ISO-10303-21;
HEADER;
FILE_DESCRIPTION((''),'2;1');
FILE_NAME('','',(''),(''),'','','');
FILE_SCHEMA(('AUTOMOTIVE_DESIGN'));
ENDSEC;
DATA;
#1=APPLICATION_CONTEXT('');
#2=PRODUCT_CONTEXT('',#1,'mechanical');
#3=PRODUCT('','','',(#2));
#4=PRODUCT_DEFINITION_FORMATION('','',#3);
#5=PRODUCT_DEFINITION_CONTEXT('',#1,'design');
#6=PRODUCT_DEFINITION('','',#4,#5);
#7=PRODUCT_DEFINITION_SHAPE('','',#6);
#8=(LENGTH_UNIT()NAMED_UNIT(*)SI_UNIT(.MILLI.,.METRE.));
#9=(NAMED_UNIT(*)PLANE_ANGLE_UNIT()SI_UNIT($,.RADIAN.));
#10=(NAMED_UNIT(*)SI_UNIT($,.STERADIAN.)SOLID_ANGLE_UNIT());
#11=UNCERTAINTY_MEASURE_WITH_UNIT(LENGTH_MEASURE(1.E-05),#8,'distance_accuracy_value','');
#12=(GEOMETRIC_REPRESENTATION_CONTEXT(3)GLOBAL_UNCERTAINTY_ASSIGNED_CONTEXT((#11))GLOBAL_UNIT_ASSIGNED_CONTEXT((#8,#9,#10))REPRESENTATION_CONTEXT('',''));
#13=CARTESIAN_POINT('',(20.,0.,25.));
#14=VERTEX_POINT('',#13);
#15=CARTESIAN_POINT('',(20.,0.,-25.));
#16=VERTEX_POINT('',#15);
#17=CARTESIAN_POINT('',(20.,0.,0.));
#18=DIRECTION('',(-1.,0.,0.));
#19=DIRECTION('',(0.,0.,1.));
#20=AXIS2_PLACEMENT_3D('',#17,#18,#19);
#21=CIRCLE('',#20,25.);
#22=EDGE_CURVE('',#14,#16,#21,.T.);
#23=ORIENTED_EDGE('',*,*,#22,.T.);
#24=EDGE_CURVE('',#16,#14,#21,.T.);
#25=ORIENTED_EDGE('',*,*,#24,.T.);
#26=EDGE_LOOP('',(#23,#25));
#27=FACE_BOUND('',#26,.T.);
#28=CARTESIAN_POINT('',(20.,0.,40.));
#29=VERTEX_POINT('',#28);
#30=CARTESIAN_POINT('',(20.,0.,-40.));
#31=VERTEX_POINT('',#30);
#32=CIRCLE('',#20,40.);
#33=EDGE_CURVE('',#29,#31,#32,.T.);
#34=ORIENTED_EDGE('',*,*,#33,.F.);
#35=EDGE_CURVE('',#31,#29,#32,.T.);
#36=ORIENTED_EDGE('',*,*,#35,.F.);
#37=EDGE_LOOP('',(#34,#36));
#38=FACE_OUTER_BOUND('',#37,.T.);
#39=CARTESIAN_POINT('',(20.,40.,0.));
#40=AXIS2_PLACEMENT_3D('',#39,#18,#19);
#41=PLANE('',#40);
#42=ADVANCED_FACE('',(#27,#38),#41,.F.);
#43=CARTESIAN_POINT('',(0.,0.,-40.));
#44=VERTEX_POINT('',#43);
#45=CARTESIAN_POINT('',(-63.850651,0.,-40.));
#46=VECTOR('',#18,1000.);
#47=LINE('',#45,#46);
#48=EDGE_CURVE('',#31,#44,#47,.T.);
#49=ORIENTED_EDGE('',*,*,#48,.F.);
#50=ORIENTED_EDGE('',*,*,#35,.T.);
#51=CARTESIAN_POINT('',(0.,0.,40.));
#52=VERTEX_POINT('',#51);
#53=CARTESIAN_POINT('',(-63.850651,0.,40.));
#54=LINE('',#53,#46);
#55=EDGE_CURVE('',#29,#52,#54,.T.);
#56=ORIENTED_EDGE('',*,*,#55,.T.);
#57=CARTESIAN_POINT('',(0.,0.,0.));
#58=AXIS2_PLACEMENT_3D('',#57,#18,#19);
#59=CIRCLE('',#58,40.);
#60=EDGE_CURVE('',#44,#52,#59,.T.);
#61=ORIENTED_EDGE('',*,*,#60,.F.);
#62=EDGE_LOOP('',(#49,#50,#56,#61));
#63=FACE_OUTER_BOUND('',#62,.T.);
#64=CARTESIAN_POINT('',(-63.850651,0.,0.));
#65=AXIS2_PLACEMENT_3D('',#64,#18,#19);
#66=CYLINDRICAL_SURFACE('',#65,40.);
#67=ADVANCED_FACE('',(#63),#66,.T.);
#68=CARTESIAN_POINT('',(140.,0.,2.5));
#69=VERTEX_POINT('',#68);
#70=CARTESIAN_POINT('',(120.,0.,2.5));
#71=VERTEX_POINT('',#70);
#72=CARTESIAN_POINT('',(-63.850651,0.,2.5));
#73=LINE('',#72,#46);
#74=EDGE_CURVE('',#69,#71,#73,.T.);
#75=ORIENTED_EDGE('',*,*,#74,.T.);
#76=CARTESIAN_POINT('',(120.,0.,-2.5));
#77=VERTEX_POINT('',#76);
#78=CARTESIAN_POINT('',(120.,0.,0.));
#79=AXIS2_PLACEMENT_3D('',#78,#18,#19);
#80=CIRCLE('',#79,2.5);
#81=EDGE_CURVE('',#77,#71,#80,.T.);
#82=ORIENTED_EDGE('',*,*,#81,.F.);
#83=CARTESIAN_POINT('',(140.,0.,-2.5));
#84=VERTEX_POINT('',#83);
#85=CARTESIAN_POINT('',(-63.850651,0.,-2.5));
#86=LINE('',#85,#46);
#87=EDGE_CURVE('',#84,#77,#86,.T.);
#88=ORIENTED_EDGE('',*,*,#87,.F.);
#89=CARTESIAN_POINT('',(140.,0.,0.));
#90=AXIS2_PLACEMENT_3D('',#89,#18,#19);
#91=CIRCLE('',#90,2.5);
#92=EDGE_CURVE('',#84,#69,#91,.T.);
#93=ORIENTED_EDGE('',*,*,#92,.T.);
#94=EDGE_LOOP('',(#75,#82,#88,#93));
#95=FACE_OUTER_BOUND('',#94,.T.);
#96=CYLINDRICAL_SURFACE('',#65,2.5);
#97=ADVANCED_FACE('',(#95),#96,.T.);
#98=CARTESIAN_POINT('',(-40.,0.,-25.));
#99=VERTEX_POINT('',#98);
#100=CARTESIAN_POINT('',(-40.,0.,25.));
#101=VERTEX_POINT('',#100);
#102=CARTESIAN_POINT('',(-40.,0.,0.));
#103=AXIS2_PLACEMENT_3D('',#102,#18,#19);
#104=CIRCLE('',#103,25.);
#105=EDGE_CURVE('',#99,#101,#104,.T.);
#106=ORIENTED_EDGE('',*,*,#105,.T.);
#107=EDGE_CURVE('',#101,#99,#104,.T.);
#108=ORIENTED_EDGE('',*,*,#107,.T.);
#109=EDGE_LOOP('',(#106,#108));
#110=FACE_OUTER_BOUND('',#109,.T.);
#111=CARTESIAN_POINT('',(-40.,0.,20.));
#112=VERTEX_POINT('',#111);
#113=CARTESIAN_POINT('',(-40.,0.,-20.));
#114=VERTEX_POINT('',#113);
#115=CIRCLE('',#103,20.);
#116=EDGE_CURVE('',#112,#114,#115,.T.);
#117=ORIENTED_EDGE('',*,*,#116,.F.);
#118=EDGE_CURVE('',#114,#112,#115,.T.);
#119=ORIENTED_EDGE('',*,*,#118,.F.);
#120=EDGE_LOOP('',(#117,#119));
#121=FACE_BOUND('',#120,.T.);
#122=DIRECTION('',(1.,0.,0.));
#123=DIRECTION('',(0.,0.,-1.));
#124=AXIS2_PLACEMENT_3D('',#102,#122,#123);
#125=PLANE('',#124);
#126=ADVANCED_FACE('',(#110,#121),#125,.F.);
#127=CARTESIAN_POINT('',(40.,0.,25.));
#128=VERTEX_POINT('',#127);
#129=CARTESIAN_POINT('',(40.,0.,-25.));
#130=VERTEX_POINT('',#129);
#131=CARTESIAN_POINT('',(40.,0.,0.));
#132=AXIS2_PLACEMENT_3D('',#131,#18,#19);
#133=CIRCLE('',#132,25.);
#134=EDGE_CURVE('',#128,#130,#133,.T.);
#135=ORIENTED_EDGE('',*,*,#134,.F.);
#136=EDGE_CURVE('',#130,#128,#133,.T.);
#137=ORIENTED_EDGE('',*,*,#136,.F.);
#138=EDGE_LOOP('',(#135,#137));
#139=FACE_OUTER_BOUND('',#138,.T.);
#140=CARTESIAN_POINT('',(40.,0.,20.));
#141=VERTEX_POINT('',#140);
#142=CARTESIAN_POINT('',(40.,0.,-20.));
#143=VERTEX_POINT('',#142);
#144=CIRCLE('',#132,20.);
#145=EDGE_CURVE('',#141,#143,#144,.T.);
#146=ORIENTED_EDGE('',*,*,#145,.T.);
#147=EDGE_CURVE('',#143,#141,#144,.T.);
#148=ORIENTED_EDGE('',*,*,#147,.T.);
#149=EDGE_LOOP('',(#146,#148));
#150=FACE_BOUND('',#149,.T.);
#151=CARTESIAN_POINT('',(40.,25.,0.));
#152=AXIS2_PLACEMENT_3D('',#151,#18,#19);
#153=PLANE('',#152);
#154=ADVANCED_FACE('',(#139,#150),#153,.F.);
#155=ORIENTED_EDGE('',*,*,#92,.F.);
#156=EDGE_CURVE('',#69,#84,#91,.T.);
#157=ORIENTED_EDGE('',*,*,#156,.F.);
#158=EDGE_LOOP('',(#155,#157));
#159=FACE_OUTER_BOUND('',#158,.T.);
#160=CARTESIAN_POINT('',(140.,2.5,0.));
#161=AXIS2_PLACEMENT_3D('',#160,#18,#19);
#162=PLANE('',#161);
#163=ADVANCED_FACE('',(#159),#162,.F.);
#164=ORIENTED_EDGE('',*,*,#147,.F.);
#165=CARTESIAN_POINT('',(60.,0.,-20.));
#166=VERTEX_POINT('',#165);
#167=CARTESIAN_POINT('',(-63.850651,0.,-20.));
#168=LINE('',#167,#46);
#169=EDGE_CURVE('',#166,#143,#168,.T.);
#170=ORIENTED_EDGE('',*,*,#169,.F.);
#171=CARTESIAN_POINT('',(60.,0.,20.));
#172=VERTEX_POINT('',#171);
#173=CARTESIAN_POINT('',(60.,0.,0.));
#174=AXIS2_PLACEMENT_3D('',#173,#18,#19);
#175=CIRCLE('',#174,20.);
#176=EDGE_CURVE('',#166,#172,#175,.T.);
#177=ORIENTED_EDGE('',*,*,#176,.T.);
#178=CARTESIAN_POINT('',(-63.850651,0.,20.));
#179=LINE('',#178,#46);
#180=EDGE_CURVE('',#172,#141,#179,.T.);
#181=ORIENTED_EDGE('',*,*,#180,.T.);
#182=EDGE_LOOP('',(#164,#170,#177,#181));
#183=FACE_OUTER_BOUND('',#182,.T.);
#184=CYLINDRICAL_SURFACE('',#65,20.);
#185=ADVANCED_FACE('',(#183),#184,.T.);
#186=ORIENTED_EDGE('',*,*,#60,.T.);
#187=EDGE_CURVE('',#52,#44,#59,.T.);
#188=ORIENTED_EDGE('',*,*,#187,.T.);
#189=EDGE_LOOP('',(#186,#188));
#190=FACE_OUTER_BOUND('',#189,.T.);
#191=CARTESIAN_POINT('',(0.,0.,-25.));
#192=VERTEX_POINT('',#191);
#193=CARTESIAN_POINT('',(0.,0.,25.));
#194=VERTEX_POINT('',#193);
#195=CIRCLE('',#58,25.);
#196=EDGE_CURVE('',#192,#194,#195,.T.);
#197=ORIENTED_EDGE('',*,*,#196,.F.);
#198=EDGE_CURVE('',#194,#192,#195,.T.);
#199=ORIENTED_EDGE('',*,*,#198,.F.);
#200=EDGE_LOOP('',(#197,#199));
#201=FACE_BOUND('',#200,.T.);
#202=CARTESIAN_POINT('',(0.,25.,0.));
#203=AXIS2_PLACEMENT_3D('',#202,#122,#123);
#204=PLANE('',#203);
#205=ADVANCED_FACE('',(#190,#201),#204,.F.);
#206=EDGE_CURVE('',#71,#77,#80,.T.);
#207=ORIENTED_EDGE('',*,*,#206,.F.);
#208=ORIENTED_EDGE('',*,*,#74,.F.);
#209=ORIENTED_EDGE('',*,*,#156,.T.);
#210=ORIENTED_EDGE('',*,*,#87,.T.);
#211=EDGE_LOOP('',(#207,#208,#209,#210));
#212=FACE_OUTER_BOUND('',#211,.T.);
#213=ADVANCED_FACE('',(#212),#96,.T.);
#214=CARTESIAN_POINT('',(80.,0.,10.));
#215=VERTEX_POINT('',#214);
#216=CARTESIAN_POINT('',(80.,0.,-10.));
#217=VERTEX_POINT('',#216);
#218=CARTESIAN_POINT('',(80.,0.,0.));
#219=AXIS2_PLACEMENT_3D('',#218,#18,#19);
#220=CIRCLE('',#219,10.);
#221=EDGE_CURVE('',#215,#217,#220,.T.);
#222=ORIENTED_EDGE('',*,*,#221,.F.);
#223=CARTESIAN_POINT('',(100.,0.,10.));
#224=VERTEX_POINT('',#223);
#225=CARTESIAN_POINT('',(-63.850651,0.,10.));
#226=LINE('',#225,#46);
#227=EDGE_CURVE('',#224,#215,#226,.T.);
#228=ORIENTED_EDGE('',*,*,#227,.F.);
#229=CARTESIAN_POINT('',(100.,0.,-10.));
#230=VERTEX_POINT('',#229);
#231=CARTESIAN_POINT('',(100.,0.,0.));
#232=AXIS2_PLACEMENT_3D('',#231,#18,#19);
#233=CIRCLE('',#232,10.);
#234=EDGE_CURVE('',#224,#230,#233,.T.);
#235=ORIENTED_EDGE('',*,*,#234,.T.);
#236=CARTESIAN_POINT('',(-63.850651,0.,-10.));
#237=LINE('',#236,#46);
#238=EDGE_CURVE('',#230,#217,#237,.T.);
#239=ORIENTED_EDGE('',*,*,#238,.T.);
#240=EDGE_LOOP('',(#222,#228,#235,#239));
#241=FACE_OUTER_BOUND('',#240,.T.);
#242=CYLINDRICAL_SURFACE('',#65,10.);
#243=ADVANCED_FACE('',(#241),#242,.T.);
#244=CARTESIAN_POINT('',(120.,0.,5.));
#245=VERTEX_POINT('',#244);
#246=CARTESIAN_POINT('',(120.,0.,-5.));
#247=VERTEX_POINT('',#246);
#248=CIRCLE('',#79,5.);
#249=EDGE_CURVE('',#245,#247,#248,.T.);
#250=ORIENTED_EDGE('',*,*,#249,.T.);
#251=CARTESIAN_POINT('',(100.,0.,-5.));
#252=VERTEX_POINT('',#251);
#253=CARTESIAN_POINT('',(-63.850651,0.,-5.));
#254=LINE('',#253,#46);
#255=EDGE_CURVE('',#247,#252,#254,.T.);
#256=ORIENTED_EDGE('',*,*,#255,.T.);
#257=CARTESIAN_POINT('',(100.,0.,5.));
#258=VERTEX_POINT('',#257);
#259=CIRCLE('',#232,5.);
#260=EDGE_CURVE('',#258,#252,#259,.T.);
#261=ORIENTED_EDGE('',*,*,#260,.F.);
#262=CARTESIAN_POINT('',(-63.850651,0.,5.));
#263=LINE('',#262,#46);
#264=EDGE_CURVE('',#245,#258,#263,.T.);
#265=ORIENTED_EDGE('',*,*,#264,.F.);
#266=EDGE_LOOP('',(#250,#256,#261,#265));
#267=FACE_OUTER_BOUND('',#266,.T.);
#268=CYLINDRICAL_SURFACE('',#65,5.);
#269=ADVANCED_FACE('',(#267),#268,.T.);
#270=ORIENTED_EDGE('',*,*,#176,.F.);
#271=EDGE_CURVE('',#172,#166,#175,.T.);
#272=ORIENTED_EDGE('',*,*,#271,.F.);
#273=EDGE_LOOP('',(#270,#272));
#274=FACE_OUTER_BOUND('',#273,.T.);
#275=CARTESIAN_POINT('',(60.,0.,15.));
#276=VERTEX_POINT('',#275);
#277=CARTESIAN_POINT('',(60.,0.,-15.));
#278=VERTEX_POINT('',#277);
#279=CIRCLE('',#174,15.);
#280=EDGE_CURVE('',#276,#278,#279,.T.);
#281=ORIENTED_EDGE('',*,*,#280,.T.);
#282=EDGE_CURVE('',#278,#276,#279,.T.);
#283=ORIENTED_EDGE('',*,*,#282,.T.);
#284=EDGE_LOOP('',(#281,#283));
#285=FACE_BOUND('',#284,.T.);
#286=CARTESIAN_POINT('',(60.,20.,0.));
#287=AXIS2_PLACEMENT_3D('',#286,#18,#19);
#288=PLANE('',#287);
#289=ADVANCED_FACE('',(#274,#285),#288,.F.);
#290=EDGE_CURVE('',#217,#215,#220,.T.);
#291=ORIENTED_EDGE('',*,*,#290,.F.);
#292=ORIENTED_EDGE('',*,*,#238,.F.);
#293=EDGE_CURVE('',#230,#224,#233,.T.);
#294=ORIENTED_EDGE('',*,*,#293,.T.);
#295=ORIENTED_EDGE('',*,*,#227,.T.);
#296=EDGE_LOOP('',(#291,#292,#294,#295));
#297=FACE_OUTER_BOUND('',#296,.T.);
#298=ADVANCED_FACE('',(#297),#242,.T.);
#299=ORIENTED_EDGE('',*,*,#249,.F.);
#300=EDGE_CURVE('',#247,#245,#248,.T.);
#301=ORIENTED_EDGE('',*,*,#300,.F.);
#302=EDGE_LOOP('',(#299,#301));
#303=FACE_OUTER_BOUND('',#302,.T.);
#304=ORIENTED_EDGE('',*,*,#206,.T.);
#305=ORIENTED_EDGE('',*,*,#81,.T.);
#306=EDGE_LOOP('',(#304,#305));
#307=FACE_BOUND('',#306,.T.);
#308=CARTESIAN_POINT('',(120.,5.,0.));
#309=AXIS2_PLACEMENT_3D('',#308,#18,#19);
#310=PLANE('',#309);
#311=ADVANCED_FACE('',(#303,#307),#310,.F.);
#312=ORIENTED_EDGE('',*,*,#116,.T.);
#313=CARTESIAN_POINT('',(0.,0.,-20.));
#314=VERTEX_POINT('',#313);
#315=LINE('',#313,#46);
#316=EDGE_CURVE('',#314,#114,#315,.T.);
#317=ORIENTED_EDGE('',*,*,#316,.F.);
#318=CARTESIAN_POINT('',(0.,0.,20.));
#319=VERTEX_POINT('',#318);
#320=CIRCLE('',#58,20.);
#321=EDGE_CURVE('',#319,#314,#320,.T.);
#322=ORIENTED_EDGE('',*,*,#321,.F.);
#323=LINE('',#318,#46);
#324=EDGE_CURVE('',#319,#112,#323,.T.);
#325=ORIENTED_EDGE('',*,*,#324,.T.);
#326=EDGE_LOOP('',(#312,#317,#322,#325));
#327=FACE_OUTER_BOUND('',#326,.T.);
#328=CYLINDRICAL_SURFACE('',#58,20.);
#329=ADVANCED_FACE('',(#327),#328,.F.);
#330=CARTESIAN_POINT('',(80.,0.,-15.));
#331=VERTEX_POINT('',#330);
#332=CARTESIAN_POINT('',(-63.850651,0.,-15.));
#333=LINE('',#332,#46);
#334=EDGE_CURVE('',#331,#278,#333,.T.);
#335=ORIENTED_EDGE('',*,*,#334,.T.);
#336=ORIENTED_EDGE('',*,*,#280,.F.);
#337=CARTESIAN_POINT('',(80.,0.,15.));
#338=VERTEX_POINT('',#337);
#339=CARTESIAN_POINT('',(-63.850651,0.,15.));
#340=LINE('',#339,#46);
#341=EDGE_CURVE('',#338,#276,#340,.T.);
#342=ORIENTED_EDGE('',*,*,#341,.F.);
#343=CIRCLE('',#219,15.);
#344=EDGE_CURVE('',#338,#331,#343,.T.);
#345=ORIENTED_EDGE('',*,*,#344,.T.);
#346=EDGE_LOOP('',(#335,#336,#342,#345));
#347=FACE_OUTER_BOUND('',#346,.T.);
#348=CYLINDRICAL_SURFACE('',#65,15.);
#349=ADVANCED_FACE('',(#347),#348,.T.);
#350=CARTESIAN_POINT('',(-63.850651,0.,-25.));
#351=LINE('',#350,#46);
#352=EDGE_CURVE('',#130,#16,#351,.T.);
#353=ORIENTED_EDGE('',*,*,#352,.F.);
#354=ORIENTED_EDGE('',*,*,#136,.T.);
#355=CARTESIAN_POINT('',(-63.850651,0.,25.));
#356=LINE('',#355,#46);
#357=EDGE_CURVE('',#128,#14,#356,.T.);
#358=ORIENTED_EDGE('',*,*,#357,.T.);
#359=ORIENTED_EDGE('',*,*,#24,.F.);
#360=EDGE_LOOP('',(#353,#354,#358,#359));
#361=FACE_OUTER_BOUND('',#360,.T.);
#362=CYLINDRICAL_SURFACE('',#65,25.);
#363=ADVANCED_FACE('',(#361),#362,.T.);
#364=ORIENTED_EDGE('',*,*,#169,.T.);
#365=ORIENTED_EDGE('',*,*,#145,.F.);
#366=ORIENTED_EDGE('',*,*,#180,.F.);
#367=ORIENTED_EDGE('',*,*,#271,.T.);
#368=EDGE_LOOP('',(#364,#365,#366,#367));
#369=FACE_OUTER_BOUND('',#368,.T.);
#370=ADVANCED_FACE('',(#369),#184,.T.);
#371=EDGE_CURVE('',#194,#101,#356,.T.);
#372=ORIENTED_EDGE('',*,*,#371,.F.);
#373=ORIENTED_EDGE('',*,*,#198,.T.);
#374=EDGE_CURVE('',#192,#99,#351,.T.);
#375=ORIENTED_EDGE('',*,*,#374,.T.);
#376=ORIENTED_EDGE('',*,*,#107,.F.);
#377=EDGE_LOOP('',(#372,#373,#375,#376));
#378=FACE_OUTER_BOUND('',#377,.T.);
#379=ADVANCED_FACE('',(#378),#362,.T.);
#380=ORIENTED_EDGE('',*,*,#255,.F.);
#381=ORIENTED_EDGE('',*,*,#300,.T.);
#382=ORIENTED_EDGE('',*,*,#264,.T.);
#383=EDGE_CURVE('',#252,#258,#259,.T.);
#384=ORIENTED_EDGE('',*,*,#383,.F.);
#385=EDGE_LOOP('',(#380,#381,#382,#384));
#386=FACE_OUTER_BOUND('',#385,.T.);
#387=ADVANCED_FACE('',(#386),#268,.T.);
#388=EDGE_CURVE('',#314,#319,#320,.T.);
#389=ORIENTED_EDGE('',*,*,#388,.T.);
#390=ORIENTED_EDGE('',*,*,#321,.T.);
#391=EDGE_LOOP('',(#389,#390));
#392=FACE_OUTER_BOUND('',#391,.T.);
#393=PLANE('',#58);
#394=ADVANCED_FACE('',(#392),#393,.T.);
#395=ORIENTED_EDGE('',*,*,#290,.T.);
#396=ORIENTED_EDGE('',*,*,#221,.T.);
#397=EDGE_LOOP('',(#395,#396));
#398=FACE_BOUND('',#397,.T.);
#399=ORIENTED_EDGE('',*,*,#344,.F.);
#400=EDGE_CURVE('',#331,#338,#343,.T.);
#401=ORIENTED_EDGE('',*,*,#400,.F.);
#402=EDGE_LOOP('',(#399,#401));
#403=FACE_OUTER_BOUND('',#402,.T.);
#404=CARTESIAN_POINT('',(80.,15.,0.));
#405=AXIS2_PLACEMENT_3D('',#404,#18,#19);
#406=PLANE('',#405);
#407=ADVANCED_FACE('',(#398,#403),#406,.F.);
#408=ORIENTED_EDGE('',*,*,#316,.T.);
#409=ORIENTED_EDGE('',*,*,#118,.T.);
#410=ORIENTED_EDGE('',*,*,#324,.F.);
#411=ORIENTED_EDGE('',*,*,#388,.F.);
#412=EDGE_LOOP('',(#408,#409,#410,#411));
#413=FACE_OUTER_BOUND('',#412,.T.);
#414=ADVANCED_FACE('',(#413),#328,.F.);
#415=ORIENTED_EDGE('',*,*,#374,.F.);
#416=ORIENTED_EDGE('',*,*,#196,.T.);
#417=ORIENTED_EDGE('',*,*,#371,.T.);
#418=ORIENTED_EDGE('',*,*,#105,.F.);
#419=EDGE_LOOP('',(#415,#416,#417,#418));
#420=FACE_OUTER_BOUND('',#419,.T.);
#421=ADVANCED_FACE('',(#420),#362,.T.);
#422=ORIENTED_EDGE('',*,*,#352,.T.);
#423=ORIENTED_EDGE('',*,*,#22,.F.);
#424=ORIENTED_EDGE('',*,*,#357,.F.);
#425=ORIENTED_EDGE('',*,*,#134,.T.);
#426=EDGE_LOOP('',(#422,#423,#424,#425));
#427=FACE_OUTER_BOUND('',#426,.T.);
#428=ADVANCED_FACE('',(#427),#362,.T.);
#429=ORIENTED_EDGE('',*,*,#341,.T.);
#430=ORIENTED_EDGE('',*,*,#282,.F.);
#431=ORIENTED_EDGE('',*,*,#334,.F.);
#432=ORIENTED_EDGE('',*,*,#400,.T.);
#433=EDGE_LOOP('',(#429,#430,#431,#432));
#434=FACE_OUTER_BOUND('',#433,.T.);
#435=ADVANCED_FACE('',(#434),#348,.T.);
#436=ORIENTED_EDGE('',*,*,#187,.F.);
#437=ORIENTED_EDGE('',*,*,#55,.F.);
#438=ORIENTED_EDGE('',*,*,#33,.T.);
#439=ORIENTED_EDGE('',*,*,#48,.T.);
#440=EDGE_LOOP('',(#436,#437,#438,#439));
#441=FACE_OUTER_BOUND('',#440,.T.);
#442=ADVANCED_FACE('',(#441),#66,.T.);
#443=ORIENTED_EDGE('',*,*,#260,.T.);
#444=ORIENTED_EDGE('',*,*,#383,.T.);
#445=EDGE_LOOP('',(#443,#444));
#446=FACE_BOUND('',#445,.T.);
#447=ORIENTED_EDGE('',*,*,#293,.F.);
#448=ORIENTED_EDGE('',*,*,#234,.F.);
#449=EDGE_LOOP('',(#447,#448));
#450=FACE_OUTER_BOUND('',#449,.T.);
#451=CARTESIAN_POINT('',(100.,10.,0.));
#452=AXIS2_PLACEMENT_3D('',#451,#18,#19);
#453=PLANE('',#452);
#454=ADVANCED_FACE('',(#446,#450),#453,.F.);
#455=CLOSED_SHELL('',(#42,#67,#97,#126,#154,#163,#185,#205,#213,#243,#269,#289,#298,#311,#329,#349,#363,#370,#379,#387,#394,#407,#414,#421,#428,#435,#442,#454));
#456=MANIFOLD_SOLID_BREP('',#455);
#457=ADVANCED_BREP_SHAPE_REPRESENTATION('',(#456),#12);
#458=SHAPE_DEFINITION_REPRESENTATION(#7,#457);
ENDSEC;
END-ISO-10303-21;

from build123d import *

# Parameters (mm, degrees)
END_START             = -40
END_CUT_SKETCH_40_R   = 20
END_CUT_40_X_40_DEPTH = 40


with BuildPart() as part:
    # Shaft Profile Sketch → Stepped Shaft Revolve (revolve)
    with BuildSketch(Plane.XY, mode=Mode.PRIVATE) as stepped_shaft_revolve_sk:
        Polygon((-40, 0), (-40, 25), (0, 25), (0, 40), (20, 40), (20, 25), (40, 25), (40, 20), (60, 20), (60, 15), (80, 15), (80, 10), (100, 10), (100, 5), (120, 5), (120, 2.5), (140, 2.5), (140, 0), align=None)
    revolve(stepped_shaft_revolve_sk.sketch.rotate(Axis((-63.850651288, 0, 0), (1, 0, 0)), 90), axis=Axis((-63.850651288, 0, 0), (1, 0, 0)))

    # End Cut Sketch Ø40 → End Cut Ø40 x 40 (cut)
    with BuildSketch(Plane.ZY.offset(40).offset(END_START)):
        Circle(END_CUT_SKETCH_40_R)
    extrude(amount=END_CUT_40_X_40_DEPTH, mode=Mode.SUBTRACT)


solid = part.part
